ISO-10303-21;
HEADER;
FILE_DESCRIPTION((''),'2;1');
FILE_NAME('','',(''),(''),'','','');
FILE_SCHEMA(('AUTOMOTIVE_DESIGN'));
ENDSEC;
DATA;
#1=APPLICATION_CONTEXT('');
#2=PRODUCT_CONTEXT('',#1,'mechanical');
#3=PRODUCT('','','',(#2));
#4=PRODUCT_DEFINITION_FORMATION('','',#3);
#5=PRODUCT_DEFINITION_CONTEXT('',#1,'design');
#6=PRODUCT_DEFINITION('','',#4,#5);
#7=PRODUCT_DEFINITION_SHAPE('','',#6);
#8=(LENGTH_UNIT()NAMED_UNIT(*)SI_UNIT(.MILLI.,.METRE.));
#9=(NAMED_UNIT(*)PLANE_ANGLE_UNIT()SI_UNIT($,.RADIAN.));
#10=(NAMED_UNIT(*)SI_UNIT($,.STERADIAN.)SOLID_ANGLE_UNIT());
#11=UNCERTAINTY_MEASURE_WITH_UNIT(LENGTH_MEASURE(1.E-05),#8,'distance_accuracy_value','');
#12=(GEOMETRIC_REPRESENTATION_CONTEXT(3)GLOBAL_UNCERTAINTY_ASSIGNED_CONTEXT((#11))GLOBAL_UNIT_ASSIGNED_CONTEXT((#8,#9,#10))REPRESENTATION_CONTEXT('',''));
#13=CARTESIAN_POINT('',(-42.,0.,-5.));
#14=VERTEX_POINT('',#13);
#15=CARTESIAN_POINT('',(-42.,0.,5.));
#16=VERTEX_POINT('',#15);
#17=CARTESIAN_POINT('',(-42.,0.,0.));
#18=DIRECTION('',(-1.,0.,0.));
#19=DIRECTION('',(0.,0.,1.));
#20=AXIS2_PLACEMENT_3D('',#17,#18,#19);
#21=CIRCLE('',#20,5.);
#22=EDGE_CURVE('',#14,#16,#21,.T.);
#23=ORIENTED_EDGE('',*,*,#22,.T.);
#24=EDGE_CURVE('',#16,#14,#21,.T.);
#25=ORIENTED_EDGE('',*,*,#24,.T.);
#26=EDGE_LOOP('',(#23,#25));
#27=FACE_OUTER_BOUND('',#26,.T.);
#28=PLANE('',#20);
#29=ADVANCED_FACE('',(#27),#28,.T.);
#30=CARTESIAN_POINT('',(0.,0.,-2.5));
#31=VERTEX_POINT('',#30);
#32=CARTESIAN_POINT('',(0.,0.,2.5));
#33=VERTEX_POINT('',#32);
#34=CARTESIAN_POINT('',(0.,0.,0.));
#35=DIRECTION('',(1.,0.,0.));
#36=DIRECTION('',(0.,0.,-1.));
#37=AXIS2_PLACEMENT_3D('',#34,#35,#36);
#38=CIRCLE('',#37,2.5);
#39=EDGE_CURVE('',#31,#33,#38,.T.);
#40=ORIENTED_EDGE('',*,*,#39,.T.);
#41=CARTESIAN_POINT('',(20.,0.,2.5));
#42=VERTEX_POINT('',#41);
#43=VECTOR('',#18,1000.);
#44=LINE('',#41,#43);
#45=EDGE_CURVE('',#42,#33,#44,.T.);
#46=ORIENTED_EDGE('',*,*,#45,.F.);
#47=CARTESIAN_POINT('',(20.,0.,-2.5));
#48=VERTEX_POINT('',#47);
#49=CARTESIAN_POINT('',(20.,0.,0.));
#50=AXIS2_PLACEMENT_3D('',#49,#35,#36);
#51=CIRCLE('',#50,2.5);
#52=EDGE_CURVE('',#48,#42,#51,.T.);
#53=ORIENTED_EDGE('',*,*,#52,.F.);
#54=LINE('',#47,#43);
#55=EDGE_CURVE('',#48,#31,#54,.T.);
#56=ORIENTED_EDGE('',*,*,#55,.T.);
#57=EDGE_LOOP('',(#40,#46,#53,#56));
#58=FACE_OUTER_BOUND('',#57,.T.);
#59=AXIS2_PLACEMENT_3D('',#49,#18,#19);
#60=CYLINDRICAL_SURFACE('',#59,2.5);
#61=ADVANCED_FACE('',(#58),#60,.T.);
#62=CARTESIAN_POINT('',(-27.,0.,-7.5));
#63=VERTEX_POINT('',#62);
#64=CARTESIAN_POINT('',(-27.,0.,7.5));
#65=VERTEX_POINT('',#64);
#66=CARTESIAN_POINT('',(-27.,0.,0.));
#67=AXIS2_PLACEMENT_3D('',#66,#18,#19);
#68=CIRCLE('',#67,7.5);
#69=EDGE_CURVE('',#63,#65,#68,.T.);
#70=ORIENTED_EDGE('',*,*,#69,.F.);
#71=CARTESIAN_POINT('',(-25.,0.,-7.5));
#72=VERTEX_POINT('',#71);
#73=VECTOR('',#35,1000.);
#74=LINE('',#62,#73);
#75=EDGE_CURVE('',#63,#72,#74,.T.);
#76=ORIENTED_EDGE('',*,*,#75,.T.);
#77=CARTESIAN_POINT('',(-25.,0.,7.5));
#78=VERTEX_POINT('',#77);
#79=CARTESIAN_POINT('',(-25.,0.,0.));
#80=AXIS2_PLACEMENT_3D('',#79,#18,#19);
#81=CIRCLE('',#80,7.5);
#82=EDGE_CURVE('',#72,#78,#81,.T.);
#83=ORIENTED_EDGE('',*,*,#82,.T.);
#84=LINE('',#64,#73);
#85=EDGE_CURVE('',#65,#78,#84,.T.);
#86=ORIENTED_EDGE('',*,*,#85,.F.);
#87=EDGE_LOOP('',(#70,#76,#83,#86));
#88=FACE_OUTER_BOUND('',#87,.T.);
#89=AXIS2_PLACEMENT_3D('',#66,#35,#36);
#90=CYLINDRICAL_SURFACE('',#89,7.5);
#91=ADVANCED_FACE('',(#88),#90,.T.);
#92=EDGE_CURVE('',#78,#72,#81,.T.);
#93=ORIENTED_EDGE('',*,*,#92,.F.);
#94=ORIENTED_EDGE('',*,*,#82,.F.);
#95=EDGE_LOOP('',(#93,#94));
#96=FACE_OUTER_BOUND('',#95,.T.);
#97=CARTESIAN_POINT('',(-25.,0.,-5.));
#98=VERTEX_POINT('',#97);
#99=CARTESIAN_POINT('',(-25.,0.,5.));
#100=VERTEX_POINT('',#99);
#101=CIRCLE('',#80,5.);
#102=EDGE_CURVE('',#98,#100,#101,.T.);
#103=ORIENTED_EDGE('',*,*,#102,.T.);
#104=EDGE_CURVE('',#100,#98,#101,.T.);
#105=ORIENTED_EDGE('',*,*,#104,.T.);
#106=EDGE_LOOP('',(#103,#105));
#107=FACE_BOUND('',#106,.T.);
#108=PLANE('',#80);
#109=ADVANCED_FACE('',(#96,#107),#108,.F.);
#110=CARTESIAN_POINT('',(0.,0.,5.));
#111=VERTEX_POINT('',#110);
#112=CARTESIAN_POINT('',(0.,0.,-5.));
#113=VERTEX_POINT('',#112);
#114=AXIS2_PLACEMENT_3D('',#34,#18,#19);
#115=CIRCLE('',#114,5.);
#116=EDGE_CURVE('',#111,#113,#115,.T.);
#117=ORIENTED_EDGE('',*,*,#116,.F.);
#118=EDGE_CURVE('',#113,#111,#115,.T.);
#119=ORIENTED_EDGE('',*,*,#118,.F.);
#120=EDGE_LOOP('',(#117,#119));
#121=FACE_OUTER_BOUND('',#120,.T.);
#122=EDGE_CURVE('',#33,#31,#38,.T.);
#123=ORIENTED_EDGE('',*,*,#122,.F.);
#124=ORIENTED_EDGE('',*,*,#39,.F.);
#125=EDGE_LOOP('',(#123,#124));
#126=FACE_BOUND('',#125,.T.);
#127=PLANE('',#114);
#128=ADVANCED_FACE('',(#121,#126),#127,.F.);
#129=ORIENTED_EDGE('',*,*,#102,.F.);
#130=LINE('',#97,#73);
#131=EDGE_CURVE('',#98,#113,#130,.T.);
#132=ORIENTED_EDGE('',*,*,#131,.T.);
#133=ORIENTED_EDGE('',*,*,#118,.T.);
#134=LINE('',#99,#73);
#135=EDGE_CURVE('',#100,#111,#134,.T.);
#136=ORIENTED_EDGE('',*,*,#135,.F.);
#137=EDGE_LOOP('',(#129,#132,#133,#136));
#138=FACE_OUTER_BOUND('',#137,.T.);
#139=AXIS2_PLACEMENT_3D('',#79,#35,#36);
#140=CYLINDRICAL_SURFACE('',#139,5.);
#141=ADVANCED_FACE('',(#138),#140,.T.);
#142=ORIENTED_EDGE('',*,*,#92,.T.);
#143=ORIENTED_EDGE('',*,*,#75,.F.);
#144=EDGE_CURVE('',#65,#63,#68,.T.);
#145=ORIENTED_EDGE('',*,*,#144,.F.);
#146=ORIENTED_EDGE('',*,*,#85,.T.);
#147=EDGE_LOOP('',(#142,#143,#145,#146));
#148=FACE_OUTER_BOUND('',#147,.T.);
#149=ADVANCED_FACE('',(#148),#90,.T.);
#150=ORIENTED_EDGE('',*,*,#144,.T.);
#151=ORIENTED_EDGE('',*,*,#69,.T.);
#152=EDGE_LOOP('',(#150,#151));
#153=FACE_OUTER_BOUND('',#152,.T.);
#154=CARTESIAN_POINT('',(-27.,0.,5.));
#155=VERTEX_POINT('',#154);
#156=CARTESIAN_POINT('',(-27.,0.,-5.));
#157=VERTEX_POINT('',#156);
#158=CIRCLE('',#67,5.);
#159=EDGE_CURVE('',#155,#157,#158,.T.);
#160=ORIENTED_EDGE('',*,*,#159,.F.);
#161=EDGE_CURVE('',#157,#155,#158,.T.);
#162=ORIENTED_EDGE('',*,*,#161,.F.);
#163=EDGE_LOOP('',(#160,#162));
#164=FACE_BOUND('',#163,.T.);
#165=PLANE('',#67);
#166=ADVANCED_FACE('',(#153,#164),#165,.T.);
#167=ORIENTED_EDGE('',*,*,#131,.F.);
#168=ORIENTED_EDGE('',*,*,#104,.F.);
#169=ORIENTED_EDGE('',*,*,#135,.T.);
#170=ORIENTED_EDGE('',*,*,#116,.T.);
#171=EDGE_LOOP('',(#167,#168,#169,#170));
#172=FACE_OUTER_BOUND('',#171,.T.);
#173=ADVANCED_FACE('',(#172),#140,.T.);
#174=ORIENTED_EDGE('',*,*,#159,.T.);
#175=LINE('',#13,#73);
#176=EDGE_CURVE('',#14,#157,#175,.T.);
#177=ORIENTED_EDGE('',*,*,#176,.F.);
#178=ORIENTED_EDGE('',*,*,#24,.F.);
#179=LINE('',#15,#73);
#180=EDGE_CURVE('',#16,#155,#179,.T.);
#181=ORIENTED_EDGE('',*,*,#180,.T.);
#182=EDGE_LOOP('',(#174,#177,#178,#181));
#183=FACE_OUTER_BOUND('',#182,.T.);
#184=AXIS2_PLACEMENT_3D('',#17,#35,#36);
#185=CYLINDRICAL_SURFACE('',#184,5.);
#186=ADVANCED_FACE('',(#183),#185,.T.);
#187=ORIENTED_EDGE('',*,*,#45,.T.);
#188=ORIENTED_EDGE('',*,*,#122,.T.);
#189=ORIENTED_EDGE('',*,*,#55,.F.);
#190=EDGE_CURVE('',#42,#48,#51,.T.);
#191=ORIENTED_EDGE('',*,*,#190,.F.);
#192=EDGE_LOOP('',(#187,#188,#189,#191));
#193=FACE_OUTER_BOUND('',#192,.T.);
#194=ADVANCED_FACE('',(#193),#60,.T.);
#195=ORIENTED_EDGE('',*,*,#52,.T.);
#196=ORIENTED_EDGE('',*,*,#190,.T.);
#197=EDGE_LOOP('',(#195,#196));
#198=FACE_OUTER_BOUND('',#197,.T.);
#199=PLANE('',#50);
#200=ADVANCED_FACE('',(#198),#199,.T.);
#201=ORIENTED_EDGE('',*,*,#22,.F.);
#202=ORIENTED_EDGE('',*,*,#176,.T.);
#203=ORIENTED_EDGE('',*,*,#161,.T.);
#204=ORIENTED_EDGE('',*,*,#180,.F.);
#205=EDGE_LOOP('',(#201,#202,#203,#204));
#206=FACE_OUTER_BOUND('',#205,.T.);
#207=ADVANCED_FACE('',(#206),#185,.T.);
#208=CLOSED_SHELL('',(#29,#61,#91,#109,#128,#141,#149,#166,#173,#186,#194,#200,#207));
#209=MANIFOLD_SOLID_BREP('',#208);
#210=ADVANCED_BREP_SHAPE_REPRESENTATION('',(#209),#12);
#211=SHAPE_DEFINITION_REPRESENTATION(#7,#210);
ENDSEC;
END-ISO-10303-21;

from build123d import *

# Parameters (mm, degrees)
SKETCH_1_R      = 2.5
EXTRUDE_1_DEPTH = 20
SKETCH_2_R      = 5
EXTRUDE_2_DEPTH = 25
SKETCH_3_R      = 7.5
EXTRUDE_3_DEPTH = 2
SKETCH_4_R      = 5
EXTRUDE_4_DEPTH = 15


with BuildPart() as part:
    # 草图1 → 凸台-拉伸1 (new body)
    with BuildSketch(Plane(origin=(0, 0, 0), x_dir=(0, 0, -1), z_dir=(1, 0, 0))):
        Circle(SKETCH_1_R)
    extrude(amount=EXTRUDE_1_DEPTH)

    # 草图2 → 凸台-拉伸2 (add)
    with BuildSketch(Plane.ZY):
        Circle(SKETCH_2_R)
    extrude(amount=EXTRUDE_2_DEPTH)

    # 草图3 → 凸台-拉伸3 (add)
    with BuildSketch(Plane.ZY.offset(25)):
        Circle(SKETCH_3_R)
    extrude(amount=EXTRUDE_3_DEPTH)

    # 草图4 → 凸台-拉伸4 (add)
    with BuildSketch(Plane.ZY.offset(27)):
        Circle(SKETCH_4_R)
    extrude(amount=EXTRUDE_4_DEPTH)


solid = part.part
